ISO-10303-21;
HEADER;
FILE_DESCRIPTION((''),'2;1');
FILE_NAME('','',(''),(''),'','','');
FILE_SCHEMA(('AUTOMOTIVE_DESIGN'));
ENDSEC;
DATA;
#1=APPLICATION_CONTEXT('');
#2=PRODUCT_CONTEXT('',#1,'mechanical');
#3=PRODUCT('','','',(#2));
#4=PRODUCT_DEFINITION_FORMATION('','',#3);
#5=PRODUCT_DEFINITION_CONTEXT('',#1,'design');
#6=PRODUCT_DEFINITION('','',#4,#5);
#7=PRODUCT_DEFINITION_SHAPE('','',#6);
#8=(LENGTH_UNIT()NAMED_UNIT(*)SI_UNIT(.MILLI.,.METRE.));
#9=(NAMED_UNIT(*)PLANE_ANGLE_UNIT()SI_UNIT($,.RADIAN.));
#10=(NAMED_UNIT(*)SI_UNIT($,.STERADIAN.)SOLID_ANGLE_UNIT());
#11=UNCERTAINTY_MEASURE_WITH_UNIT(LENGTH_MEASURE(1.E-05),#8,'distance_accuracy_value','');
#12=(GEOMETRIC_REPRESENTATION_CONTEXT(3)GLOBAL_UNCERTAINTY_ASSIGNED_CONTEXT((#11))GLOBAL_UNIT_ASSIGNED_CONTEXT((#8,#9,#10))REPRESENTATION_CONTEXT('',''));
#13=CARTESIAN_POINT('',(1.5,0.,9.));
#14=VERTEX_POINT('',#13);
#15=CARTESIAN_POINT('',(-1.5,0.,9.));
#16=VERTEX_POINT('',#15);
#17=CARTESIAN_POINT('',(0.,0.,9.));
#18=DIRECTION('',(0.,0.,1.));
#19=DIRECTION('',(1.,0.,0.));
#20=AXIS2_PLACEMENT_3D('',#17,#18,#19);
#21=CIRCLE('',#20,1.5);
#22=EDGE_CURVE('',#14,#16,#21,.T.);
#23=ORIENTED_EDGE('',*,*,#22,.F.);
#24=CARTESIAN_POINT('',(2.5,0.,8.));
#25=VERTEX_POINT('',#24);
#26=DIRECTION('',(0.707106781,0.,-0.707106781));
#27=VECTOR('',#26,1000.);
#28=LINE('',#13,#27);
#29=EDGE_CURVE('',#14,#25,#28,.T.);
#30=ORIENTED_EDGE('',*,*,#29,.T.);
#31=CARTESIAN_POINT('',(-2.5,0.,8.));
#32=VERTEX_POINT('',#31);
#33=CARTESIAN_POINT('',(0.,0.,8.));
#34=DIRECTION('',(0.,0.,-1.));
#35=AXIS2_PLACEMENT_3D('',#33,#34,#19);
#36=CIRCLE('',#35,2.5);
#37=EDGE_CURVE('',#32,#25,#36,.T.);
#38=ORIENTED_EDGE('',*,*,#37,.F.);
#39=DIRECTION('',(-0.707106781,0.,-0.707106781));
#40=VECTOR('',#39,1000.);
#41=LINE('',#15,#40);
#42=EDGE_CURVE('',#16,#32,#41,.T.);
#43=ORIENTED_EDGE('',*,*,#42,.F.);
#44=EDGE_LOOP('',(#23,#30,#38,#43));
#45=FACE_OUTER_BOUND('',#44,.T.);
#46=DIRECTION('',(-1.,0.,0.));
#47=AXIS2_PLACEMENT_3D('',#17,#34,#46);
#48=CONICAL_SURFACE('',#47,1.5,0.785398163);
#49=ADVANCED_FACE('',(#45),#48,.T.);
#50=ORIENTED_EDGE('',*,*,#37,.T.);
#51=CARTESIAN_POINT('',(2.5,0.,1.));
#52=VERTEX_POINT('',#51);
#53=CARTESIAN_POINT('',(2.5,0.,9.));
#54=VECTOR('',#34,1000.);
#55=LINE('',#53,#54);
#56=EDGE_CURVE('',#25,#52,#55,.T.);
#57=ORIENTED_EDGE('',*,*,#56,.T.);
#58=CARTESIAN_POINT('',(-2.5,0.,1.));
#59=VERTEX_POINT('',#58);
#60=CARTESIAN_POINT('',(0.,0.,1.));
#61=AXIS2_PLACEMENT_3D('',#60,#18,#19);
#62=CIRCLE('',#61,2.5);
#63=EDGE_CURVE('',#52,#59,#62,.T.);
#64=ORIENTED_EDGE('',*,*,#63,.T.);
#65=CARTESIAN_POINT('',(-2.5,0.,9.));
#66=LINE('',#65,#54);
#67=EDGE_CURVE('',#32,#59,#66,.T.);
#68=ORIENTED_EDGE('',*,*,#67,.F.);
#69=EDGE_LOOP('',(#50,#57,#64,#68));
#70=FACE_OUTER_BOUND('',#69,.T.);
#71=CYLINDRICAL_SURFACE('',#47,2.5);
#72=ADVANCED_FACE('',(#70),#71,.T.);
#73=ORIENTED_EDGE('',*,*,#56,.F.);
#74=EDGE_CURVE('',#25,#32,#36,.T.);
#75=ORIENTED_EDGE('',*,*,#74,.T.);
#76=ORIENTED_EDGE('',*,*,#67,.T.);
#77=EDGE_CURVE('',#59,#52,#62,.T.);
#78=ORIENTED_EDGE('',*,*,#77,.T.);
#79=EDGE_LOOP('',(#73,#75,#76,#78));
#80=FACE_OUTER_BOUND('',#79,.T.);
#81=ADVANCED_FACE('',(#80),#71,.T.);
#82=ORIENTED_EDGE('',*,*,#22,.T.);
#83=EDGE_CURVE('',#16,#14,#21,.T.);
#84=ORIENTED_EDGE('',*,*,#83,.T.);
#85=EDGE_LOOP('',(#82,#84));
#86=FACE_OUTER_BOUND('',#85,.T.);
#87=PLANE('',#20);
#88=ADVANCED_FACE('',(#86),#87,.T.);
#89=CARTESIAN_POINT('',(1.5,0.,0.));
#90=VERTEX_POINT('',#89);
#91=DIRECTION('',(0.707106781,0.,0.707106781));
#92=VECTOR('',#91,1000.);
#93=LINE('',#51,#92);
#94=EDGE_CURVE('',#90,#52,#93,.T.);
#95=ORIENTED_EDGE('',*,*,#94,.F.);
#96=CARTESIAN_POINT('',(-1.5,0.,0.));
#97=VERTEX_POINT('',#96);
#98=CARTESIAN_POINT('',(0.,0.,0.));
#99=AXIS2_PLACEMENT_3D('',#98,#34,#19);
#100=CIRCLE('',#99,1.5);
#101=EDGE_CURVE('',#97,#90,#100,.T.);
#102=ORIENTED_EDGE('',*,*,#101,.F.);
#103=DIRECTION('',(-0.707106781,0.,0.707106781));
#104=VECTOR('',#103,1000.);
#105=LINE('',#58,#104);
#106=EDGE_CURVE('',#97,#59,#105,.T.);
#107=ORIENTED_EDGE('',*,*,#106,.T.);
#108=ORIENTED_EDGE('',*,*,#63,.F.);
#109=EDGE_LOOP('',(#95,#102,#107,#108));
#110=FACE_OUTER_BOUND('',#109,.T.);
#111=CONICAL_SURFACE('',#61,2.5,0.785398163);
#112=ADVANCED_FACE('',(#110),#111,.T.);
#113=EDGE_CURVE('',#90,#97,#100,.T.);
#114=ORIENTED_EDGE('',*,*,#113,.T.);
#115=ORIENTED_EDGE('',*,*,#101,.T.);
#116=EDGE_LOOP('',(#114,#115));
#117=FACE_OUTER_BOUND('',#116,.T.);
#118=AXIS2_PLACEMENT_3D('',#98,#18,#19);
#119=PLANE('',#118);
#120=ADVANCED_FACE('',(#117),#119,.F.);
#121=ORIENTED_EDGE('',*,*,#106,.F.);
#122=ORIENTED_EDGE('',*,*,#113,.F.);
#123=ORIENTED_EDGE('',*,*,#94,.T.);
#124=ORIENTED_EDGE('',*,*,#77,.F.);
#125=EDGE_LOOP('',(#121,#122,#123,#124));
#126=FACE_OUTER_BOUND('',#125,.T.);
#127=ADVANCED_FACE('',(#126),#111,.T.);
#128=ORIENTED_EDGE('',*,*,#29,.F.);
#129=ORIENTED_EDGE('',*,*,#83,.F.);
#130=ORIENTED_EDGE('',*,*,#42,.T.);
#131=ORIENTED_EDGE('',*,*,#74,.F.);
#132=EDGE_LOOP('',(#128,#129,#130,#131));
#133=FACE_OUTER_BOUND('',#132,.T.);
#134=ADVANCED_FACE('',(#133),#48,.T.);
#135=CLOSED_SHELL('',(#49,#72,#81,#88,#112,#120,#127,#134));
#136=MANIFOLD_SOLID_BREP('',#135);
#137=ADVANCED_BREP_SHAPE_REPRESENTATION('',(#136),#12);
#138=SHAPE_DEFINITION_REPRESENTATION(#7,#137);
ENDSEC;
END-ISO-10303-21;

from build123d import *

# Parameters (mm, degrees)
SKETCH1_R           = 2.5
BOSS_EXTRUDE1_DEPTH = 9
CHAMFER1_SIZE       = 1


with BuildPart() as part:
    # Sketch1 → Boss-Extrude1 (new body)
    with BuildSketch(Plane.XY):
        Circle(SKETCH1_R)
    extrude(amount=BOSS_EXTRUDE1_DEPTH)

    # Chamfer1
    chamfer1_edges = [part.edges().sort_by_distance(p)[0] for p in [
        (-2.5, 0, 0),
        (-2.5, 0, 9),
    ]]
    chamfer(chamfer1_edges, length=CHAMFER1_SIZE)


solid = part.part
